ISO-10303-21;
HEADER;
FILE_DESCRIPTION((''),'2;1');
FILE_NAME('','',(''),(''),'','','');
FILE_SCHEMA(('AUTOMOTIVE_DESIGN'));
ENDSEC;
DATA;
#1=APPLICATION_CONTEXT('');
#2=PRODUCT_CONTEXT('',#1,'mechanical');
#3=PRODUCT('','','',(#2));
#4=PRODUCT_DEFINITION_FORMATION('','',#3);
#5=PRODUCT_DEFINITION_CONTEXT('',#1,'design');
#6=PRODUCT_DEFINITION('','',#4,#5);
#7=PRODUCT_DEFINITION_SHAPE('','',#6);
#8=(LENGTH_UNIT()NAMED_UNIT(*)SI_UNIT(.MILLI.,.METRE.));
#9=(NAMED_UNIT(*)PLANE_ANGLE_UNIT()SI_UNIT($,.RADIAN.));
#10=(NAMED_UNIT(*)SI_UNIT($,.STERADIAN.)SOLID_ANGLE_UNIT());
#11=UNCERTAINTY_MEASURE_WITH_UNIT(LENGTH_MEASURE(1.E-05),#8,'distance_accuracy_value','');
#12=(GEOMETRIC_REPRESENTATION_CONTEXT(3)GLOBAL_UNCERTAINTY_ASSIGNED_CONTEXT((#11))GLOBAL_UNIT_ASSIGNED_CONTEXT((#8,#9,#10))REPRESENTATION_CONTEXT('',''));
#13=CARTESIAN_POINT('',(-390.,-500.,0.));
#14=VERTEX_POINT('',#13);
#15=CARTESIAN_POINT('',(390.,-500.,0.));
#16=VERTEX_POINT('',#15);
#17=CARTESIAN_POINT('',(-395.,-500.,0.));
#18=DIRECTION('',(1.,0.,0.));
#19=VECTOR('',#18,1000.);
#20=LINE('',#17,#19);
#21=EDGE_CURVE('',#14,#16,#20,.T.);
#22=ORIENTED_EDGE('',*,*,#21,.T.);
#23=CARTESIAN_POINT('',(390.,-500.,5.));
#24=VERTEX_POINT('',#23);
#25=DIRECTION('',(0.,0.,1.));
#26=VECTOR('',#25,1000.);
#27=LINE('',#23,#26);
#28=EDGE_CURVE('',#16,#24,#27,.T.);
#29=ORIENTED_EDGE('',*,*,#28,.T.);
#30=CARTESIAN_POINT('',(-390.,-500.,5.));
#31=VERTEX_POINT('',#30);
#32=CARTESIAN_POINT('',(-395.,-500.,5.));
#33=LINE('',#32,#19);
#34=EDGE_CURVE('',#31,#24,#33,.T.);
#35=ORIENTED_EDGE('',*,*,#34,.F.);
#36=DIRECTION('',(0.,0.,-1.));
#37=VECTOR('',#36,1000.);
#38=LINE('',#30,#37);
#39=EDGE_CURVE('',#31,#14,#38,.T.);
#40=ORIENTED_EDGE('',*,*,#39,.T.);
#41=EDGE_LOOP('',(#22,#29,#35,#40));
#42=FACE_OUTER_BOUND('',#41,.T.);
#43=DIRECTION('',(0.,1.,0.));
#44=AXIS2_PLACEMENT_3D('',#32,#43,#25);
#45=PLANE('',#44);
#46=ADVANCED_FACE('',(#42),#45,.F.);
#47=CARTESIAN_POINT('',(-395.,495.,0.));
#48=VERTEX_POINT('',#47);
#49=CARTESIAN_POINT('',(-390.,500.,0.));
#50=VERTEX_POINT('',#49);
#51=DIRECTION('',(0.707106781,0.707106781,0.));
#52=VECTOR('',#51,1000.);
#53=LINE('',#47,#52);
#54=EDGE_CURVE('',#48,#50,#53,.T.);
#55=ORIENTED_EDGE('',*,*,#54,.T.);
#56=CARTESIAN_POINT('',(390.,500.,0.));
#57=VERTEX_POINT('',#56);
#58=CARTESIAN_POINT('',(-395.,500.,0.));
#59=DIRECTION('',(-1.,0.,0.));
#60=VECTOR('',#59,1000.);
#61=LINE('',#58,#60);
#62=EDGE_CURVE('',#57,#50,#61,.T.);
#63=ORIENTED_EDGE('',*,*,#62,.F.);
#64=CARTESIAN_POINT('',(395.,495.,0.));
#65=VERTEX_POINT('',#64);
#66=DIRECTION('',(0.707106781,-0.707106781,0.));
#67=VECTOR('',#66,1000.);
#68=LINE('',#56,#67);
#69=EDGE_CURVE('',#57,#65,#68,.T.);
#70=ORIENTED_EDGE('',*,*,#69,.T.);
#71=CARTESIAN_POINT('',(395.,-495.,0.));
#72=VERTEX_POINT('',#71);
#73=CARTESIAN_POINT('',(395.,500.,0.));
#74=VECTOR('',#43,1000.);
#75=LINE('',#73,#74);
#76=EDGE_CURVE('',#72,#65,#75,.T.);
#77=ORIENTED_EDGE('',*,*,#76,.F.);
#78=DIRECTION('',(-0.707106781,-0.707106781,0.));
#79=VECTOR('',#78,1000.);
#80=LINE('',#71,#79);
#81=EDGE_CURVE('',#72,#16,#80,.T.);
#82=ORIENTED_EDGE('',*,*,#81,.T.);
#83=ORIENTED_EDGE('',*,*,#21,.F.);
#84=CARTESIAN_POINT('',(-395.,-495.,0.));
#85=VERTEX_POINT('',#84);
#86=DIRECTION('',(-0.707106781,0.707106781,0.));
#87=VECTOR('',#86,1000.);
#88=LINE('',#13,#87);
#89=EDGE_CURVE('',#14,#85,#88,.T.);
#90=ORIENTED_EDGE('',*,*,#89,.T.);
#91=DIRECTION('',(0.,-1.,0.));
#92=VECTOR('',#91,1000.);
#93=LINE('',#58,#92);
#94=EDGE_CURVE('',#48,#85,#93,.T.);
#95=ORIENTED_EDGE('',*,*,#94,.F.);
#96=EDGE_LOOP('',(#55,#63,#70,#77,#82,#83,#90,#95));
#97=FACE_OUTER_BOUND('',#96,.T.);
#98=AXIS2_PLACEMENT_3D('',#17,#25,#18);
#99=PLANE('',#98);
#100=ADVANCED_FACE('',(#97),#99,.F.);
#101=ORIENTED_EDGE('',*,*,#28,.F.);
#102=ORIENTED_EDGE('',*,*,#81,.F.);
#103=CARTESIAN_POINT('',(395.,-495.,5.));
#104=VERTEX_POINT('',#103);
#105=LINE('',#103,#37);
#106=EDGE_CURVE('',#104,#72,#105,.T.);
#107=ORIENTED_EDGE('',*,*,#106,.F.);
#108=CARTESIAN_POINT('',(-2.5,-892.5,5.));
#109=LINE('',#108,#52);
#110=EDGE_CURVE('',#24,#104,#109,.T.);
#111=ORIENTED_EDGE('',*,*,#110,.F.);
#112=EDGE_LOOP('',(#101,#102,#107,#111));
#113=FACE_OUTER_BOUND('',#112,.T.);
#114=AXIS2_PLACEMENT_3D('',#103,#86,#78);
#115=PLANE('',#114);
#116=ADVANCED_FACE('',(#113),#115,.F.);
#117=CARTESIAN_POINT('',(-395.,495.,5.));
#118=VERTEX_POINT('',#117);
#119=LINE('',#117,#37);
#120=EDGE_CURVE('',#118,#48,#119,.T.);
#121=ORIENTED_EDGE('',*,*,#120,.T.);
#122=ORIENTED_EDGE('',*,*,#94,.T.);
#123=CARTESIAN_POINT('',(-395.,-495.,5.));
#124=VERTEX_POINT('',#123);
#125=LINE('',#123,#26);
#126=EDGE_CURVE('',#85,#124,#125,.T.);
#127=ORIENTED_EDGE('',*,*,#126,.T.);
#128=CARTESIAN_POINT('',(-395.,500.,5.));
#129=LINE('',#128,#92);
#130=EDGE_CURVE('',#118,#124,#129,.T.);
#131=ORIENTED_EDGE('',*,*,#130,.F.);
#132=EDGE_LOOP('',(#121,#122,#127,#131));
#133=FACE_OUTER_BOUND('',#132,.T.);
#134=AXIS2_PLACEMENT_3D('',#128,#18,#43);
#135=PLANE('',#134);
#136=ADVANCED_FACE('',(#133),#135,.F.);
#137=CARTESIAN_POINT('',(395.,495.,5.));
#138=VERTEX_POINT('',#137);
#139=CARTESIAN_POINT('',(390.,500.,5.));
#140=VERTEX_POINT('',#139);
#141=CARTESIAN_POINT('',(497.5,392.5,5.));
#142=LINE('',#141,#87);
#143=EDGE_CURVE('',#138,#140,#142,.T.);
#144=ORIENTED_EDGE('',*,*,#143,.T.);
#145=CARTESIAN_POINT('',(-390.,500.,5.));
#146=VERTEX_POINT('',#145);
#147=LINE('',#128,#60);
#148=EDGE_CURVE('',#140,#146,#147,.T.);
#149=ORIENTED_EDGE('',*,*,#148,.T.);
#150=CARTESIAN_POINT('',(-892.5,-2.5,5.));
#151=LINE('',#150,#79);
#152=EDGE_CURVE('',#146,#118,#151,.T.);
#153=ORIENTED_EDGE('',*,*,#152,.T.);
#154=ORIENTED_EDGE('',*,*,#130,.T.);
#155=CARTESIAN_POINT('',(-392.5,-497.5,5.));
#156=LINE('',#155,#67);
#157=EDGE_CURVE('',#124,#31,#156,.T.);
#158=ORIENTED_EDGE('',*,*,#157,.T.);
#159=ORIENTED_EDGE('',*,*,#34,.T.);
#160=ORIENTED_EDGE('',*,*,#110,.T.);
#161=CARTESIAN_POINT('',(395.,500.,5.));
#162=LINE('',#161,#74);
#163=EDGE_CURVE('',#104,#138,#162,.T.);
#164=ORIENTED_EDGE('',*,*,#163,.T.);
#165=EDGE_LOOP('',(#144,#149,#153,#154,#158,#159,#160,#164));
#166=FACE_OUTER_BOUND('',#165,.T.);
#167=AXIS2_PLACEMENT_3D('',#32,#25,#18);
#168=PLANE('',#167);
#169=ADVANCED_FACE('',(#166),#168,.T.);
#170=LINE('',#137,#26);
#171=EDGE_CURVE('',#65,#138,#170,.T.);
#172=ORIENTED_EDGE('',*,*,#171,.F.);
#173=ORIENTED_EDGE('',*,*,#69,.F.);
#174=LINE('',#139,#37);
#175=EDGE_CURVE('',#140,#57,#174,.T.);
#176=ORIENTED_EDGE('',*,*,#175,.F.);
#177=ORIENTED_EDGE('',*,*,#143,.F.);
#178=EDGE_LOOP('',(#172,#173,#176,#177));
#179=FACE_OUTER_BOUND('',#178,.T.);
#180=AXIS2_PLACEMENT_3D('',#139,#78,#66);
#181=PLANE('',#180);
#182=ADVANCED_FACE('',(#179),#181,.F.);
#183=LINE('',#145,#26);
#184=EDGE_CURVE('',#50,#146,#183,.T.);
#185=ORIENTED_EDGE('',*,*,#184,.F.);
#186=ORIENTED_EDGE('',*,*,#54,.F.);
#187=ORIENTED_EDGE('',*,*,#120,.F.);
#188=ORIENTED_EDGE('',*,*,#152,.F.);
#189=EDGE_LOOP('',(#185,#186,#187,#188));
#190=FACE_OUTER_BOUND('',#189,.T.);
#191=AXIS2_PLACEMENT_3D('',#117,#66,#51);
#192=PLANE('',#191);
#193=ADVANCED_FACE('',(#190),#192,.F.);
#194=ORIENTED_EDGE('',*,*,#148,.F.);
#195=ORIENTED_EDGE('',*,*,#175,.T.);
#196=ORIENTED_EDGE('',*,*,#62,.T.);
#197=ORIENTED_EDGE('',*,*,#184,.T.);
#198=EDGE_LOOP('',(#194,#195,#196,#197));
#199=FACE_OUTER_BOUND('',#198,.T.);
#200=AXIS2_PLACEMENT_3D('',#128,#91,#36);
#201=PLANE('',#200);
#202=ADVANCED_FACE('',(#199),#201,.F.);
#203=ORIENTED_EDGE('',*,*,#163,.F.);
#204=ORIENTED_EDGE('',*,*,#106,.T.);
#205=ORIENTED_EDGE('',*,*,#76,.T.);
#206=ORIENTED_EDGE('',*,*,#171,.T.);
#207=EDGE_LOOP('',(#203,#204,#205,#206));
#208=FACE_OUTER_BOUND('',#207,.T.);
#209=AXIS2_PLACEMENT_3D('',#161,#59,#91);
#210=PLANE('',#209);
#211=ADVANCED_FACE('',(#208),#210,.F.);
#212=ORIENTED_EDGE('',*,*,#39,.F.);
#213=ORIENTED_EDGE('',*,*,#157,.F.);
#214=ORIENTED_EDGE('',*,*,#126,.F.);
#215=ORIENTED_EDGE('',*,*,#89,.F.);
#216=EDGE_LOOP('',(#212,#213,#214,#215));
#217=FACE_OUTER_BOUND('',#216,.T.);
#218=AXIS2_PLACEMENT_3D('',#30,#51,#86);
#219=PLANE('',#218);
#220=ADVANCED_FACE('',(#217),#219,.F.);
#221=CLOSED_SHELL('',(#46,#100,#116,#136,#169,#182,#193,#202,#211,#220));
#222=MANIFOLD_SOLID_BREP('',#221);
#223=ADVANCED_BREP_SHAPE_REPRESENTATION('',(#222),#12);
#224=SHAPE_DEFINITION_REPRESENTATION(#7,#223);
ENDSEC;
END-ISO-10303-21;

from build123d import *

# Parameters (mm, degrees)
SKETCH_1_W      = 790
SKETCH_1_H      = 1000
EXTRUDE_1_DEPTH = 5
CHAMFER_1_SIZE  = 5


with BuildPart() as part:
    # 草图1 → 拉伸1 (new body)
    with BuildSketch(Plane.XY):
        Rectangle(SKETCH_1_W, SKETCH_1_H)
    extrude(amount=EXTRUDE_1_DEPTH)

    # 倒角1
    chamfer_1_edges = [part.edges().sort_by_distance(p)[0] for p in [
        (-395, 500, 2.5),
        (395, 500, 2.5),
        (395, -500, 2.5),
        (-395, -500, 2.5),
    ]]
    chamfer(chamfer_1_edges, length=CHAMFER_1_SIZE)


solid = part.part
